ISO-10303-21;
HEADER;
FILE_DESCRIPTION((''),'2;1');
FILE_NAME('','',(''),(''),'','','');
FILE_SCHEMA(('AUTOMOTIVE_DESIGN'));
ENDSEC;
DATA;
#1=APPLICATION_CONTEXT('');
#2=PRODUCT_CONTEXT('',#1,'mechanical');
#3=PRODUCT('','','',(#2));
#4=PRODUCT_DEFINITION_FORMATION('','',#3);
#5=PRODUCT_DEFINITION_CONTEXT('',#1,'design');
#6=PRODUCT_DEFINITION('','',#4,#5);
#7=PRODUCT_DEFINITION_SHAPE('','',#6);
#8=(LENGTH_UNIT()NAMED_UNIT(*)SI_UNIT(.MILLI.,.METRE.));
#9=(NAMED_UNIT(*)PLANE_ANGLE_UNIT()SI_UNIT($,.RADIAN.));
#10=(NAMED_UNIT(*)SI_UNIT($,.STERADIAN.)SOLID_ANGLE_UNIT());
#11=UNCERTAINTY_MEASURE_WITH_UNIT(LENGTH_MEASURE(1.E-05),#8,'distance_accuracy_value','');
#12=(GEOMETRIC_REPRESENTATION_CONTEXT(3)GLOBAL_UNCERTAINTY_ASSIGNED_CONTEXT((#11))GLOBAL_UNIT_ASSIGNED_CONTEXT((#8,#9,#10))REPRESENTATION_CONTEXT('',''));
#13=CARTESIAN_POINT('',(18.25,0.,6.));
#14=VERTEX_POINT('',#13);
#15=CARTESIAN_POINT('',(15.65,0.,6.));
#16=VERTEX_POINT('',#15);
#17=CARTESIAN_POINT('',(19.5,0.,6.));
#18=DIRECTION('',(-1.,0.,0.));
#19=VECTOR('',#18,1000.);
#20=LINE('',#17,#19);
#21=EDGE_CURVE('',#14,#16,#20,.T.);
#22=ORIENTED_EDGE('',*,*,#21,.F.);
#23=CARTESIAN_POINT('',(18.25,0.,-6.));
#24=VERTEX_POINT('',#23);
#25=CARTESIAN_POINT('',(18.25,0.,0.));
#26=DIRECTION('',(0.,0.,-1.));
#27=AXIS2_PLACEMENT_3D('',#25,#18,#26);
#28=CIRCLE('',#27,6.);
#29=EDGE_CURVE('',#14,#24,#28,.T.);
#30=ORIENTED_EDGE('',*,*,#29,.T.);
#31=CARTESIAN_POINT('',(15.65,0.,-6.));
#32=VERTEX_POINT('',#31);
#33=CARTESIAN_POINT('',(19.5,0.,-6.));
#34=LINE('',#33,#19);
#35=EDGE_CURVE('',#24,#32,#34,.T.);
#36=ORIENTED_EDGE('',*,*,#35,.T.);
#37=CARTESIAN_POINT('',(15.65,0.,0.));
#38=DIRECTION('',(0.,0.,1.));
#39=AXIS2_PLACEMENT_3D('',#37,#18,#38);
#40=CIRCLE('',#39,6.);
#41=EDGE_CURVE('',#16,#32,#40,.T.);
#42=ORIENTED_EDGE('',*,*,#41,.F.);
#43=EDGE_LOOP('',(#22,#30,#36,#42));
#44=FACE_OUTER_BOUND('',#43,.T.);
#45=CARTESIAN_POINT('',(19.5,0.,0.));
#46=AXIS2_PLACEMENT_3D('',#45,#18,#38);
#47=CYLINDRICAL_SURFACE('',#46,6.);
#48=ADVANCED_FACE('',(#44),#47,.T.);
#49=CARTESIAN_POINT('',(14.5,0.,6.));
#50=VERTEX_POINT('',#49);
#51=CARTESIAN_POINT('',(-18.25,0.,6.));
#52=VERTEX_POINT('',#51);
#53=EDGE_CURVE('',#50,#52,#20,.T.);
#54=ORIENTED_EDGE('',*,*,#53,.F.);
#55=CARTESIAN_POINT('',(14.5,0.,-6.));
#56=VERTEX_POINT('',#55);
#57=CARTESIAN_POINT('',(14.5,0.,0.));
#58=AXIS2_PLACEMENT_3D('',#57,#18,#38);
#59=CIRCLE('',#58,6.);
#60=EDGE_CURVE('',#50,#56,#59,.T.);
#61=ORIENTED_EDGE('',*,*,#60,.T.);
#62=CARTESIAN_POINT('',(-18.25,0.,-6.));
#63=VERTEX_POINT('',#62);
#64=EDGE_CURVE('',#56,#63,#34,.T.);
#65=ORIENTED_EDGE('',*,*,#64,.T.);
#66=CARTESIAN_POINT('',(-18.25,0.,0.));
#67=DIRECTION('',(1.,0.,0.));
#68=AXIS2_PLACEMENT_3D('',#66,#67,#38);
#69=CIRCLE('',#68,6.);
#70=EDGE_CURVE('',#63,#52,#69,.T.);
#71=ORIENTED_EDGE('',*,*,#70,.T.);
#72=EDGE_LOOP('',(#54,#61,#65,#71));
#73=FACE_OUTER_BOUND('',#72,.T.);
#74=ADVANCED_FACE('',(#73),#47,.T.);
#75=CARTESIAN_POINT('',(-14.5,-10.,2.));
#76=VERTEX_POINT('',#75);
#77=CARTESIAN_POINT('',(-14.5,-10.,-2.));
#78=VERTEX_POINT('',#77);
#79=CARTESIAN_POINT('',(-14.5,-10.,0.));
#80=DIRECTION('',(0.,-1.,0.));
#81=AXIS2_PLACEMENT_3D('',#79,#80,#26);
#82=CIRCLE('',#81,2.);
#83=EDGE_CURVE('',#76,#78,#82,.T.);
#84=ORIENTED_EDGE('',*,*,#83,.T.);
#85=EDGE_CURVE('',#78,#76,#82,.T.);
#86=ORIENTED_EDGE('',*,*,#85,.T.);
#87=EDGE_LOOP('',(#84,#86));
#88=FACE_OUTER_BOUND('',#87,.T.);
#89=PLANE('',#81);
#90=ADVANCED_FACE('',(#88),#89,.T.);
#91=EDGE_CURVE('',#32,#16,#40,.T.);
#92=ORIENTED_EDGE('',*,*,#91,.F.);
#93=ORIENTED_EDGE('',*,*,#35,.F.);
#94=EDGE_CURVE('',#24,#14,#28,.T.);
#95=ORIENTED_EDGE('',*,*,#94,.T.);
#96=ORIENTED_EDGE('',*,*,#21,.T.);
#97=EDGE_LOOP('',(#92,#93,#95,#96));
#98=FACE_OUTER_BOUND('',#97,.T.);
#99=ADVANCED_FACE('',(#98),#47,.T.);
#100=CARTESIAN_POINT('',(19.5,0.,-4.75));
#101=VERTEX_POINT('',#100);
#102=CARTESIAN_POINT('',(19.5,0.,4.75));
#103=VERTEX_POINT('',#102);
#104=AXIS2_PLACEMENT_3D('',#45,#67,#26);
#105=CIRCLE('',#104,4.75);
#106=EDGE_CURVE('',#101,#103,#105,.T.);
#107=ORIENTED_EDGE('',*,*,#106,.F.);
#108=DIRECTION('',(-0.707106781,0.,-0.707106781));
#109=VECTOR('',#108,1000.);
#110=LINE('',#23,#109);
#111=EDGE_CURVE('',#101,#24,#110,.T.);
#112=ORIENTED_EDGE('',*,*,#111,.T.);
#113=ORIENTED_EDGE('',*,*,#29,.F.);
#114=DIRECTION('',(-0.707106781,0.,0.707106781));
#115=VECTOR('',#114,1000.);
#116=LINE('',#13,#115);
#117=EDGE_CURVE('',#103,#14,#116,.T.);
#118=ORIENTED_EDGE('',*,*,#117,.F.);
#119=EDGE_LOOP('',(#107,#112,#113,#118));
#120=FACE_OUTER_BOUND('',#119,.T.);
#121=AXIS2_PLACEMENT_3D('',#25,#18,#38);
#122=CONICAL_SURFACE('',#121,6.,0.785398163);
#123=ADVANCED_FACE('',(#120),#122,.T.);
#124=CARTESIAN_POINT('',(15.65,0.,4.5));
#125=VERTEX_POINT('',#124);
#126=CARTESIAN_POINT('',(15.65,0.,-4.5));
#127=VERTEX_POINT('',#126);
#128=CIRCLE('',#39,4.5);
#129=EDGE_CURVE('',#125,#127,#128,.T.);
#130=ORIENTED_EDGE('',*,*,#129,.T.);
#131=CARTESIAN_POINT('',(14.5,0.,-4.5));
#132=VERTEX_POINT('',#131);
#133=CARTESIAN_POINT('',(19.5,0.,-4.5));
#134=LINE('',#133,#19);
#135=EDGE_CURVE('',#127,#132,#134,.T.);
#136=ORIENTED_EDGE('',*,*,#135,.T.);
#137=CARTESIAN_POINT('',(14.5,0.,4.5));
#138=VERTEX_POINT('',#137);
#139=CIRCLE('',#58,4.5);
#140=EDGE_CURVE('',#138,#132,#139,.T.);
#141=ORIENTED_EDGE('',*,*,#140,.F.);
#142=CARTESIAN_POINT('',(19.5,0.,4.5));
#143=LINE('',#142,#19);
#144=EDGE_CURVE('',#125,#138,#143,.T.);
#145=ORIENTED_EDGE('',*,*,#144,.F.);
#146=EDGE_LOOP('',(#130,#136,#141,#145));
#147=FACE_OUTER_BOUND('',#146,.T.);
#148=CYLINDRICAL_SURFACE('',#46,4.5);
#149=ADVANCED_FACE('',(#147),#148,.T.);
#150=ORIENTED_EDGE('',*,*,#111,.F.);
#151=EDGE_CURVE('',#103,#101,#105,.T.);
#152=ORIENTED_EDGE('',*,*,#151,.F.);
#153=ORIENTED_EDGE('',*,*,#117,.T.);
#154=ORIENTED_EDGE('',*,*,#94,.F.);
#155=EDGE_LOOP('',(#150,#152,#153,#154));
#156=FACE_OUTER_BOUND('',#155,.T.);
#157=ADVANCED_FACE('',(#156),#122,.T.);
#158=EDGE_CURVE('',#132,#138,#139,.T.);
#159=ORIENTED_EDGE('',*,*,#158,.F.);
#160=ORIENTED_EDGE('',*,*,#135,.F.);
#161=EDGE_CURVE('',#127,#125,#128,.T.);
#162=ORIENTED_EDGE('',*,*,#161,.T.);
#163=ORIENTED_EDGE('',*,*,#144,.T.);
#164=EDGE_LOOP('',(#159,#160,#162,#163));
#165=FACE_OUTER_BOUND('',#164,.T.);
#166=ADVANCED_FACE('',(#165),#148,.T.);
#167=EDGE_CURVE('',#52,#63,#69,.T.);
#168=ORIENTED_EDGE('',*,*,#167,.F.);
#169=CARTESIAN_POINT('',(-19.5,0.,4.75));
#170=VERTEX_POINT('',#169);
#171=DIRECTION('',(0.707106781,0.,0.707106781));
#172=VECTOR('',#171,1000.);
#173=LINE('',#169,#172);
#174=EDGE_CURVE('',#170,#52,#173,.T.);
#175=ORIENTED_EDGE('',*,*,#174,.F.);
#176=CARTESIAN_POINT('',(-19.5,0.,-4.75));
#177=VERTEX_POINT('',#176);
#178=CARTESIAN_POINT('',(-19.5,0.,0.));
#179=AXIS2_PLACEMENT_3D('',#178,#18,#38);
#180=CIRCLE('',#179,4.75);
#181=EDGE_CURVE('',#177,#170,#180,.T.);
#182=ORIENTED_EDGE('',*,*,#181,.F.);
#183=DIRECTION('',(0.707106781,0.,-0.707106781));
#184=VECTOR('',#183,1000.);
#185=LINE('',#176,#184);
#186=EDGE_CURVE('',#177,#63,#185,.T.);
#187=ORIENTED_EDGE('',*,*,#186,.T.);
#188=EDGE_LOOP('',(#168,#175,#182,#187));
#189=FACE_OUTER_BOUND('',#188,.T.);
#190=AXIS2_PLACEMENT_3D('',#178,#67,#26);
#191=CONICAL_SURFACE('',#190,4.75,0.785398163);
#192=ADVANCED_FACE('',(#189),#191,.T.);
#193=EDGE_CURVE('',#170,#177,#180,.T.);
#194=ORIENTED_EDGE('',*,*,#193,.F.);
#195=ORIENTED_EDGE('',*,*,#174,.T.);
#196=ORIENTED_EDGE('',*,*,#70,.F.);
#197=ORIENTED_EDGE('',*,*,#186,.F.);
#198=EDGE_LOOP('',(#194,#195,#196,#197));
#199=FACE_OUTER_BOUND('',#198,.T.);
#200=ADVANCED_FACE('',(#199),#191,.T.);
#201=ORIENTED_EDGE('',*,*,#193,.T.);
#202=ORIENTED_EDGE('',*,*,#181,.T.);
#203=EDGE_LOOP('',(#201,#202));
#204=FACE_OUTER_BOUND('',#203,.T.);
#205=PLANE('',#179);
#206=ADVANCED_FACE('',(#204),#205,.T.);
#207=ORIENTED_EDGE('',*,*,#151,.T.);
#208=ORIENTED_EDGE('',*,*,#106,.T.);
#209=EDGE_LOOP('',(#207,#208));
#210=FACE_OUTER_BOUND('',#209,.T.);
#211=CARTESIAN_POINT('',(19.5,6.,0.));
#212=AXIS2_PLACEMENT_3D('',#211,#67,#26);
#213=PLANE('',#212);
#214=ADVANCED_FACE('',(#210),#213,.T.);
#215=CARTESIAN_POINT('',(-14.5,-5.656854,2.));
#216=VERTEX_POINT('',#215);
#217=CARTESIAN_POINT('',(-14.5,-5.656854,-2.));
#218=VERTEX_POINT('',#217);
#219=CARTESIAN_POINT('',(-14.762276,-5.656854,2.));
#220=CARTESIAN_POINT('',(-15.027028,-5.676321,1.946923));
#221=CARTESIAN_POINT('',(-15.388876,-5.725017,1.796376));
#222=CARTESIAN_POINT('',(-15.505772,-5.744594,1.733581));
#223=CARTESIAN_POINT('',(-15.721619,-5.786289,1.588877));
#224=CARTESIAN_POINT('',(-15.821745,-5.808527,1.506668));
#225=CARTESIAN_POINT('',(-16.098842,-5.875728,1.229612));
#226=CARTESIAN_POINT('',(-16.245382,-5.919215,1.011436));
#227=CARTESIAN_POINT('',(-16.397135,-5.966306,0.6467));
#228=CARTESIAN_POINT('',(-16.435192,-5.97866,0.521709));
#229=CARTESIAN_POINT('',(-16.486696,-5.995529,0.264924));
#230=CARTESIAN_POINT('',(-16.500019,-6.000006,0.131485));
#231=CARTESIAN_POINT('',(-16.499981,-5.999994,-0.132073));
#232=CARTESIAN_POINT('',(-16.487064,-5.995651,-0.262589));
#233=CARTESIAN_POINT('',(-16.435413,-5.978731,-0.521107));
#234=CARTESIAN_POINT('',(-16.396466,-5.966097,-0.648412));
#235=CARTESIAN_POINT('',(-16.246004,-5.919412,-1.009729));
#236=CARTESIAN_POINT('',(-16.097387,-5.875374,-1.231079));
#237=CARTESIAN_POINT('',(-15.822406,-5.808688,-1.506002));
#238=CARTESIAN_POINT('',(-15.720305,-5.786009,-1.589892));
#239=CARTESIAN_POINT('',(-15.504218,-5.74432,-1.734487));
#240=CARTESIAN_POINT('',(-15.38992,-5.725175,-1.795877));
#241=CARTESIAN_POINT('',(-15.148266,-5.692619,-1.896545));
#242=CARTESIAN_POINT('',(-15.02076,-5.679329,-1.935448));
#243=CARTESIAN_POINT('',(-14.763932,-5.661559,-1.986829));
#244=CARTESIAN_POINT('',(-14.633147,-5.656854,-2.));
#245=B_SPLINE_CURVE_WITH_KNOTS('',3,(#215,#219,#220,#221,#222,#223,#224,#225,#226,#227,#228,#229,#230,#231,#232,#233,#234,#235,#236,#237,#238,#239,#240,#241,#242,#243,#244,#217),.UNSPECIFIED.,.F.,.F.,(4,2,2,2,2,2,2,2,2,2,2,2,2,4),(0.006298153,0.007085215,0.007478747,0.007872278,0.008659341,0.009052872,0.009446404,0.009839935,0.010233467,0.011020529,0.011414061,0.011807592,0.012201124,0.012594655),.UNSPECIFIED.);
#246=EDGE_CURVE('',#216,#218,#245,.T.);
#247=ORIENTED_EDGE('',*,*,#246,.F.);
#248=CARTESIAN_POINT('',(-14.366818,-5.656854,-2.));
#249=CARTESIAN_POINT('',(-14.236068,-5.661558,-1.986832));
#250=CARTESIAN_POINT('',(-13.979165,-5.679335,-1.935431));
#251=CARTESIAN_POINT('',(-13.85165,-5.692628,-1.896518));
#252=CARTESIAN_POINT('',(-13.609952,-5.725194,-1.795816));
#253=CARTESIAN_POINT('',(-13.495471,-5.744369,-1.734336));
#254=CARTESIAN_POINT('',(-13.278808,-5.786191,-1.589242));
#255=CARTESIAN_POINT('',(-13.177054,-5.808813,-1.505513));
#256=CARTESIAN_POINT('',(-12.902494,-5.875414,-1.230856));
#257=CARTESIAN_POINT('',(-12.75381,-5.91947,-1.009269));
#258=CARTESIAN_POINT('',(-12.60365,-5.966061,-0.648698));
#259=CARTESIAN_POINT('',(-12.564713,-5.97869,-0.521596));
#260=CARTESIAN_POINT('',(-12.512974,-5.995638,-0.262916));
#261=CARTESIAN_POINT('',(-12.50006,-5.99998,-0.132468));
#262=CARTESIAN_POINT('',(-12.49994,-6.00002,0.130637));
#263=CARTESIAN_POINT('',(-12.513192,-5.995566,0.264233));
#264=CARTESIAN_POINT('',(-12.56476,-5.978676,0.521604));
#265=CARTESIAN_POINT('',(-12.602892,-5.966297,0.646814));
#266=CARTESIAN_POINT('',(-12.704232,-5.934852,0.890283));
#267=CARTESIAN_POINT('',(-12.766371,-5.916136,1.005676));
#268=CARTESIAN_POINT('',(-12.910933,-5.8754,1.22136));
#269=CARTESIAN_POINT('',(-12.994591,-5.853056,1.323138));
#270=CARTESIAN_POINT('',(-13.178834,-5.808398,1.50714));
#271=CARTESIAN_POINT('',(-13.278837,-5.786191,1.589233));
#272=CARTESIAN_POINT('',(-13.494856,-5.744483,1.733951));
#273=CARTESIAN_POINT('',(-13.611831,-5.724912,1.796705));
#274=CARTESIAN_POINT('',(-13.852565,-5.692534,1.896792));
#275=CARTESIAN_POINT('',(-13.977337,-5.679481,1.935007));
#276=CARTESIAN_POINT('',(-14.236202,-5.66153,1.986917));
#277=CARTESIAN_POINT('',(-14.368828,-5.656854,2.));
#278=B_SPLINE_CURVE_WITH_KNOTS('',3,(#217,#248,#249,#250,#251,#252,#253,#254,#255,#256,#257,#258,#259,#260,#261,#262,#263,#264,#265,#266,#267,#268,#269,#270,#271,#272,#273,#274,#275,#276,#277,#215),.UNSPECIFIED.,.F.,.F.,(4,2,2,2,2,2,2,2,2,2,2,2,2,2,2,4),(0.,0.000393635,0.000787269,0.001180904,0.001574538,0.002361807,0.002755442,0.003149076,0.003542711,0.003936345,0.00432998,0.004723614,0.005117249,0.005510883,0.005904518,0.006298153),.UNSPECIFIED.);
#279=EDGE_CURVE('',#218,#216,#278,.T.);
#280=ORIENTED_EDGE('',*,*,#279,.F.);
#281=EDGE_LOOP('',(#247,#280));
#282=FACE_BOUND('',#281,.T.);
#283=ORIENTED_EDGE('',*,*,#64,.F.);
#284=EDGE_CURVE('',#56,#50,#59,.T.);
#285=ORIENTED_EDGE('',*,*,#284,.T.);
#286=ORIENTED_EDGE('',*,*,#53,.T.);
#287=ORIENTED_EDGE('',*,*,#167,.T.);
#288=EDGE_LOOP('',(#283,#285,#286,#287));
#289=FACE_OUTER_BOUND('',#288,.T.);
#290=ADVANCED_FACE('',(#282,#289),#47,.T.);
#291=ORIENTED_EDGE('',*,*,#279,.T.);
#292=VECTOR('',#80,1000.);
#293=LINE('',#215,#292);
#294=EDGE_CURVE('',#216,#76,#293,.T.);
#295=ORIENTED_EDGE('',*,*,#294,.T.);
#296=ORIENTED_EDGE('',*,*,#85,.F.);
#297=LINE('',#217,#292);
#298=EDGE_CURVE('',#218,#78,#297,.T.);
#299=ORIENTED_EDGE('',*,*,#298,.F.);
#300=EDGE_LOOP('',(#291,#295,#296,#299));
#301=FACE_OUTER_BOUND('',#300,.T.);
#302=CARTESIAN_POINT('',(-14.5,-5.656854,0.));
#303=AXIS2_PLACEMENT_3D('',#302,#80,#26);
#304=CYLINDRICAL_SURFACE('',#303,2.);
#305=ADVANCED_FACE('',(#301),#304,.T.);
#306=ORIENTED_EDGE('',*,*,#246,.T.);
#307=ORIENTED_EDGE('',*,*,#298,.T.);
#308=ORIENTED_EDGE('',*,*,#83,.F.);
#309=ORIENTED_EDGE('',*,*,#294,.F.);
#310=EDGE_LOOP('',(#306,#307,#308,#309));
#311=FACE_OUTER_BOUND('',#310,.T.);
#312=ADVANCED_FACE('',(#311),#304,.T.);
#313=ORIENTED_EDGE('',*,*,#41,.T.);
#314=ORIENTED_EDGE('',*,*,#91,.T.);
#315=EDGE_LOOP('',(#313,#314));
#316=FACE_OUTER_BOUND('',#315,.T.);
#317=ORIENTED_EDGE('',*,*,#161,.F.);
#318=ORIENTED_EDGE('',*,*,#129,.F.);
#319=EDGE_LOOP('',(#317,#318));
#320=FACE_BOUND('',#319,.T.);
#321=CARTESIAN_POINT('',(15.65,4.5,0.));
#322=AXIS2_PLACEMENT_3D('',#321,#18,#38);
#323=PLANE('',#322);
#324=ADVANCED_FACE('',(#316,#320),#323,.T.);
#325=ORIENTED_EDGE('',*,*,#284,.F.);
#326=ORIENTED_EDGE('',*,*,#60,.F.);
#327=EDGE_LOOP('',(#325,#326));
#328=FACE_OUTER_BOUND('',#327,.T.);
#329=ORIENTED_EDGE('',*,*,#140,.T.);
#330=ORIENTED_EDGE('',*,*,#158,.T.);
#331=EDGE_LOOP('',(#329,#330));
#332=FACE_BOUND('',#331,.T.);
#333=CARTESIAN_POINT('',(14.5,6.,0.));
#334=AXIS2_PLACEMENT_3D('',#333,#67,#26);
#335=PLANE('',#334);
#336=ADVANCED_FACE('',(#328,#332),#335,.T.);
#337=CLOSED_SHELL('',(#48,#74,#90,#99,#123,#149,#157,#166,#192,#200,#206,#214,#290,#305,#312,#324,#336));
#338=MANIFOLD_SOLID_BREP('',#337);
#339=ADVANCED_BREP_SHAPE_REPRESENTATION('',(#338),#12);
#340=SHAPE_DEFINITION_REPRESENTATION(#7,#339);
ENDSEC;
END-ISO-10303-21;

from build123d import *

# Parameters (mm, degrees)
SKETCH_2_W     = 2
SKETCH_2_H     = 4.343145751
CHAMFER_1_SIZE = 1.25


with BuildPart() as part:
    # 草图1 → 旋转1 (revolve)
    with BuildSketch(Plane(origin=(0, 0, 0), x_dir=(-1, 0, 0), z_dir=(0, 0, -1)), mode=Mode.PRIVATE) as revolve_1_sk:
        Polygon((-19.5, 6), (-19.5, 0), (19.5, 0), (19.5, 6), (-14.5, 6), (-14.5, 4.5), (-15.65, 4.5), (-15.65, 6), align=None)
    revolve(revolve_1_sk.sketch.rotate(Axis((19.5, 0, 0), (-1, 0, 0)), 270), axis=Axis((19.5, 0, 0), (-1, 0, 0)))

    # 草图2 → 旋转2 (revolve)
    with BuildSketch(Plane(origin=(-14.5, 0, 0), x_dir=(0, 0, -1), z_dir=(1, 0, 0))):
        with Locations((1, -7.828427125)):
            Rectangle(SKETCH_2_W, SKETCH_2_H)
    revolve(axis=Axis((-14.5, -5.656854249, 0), (0, -1, 0)))

    # 倒角1
    chamfer_1_edges = [part.edges().sort_by_distance(p)[0] for p in [
        (19.5, 0, -6),
        (-19.5, 0, -6),
    ]]
    chamfer(chamfer_1_edges, length=CHAMFER_1_SIZE)


solid = part.part
